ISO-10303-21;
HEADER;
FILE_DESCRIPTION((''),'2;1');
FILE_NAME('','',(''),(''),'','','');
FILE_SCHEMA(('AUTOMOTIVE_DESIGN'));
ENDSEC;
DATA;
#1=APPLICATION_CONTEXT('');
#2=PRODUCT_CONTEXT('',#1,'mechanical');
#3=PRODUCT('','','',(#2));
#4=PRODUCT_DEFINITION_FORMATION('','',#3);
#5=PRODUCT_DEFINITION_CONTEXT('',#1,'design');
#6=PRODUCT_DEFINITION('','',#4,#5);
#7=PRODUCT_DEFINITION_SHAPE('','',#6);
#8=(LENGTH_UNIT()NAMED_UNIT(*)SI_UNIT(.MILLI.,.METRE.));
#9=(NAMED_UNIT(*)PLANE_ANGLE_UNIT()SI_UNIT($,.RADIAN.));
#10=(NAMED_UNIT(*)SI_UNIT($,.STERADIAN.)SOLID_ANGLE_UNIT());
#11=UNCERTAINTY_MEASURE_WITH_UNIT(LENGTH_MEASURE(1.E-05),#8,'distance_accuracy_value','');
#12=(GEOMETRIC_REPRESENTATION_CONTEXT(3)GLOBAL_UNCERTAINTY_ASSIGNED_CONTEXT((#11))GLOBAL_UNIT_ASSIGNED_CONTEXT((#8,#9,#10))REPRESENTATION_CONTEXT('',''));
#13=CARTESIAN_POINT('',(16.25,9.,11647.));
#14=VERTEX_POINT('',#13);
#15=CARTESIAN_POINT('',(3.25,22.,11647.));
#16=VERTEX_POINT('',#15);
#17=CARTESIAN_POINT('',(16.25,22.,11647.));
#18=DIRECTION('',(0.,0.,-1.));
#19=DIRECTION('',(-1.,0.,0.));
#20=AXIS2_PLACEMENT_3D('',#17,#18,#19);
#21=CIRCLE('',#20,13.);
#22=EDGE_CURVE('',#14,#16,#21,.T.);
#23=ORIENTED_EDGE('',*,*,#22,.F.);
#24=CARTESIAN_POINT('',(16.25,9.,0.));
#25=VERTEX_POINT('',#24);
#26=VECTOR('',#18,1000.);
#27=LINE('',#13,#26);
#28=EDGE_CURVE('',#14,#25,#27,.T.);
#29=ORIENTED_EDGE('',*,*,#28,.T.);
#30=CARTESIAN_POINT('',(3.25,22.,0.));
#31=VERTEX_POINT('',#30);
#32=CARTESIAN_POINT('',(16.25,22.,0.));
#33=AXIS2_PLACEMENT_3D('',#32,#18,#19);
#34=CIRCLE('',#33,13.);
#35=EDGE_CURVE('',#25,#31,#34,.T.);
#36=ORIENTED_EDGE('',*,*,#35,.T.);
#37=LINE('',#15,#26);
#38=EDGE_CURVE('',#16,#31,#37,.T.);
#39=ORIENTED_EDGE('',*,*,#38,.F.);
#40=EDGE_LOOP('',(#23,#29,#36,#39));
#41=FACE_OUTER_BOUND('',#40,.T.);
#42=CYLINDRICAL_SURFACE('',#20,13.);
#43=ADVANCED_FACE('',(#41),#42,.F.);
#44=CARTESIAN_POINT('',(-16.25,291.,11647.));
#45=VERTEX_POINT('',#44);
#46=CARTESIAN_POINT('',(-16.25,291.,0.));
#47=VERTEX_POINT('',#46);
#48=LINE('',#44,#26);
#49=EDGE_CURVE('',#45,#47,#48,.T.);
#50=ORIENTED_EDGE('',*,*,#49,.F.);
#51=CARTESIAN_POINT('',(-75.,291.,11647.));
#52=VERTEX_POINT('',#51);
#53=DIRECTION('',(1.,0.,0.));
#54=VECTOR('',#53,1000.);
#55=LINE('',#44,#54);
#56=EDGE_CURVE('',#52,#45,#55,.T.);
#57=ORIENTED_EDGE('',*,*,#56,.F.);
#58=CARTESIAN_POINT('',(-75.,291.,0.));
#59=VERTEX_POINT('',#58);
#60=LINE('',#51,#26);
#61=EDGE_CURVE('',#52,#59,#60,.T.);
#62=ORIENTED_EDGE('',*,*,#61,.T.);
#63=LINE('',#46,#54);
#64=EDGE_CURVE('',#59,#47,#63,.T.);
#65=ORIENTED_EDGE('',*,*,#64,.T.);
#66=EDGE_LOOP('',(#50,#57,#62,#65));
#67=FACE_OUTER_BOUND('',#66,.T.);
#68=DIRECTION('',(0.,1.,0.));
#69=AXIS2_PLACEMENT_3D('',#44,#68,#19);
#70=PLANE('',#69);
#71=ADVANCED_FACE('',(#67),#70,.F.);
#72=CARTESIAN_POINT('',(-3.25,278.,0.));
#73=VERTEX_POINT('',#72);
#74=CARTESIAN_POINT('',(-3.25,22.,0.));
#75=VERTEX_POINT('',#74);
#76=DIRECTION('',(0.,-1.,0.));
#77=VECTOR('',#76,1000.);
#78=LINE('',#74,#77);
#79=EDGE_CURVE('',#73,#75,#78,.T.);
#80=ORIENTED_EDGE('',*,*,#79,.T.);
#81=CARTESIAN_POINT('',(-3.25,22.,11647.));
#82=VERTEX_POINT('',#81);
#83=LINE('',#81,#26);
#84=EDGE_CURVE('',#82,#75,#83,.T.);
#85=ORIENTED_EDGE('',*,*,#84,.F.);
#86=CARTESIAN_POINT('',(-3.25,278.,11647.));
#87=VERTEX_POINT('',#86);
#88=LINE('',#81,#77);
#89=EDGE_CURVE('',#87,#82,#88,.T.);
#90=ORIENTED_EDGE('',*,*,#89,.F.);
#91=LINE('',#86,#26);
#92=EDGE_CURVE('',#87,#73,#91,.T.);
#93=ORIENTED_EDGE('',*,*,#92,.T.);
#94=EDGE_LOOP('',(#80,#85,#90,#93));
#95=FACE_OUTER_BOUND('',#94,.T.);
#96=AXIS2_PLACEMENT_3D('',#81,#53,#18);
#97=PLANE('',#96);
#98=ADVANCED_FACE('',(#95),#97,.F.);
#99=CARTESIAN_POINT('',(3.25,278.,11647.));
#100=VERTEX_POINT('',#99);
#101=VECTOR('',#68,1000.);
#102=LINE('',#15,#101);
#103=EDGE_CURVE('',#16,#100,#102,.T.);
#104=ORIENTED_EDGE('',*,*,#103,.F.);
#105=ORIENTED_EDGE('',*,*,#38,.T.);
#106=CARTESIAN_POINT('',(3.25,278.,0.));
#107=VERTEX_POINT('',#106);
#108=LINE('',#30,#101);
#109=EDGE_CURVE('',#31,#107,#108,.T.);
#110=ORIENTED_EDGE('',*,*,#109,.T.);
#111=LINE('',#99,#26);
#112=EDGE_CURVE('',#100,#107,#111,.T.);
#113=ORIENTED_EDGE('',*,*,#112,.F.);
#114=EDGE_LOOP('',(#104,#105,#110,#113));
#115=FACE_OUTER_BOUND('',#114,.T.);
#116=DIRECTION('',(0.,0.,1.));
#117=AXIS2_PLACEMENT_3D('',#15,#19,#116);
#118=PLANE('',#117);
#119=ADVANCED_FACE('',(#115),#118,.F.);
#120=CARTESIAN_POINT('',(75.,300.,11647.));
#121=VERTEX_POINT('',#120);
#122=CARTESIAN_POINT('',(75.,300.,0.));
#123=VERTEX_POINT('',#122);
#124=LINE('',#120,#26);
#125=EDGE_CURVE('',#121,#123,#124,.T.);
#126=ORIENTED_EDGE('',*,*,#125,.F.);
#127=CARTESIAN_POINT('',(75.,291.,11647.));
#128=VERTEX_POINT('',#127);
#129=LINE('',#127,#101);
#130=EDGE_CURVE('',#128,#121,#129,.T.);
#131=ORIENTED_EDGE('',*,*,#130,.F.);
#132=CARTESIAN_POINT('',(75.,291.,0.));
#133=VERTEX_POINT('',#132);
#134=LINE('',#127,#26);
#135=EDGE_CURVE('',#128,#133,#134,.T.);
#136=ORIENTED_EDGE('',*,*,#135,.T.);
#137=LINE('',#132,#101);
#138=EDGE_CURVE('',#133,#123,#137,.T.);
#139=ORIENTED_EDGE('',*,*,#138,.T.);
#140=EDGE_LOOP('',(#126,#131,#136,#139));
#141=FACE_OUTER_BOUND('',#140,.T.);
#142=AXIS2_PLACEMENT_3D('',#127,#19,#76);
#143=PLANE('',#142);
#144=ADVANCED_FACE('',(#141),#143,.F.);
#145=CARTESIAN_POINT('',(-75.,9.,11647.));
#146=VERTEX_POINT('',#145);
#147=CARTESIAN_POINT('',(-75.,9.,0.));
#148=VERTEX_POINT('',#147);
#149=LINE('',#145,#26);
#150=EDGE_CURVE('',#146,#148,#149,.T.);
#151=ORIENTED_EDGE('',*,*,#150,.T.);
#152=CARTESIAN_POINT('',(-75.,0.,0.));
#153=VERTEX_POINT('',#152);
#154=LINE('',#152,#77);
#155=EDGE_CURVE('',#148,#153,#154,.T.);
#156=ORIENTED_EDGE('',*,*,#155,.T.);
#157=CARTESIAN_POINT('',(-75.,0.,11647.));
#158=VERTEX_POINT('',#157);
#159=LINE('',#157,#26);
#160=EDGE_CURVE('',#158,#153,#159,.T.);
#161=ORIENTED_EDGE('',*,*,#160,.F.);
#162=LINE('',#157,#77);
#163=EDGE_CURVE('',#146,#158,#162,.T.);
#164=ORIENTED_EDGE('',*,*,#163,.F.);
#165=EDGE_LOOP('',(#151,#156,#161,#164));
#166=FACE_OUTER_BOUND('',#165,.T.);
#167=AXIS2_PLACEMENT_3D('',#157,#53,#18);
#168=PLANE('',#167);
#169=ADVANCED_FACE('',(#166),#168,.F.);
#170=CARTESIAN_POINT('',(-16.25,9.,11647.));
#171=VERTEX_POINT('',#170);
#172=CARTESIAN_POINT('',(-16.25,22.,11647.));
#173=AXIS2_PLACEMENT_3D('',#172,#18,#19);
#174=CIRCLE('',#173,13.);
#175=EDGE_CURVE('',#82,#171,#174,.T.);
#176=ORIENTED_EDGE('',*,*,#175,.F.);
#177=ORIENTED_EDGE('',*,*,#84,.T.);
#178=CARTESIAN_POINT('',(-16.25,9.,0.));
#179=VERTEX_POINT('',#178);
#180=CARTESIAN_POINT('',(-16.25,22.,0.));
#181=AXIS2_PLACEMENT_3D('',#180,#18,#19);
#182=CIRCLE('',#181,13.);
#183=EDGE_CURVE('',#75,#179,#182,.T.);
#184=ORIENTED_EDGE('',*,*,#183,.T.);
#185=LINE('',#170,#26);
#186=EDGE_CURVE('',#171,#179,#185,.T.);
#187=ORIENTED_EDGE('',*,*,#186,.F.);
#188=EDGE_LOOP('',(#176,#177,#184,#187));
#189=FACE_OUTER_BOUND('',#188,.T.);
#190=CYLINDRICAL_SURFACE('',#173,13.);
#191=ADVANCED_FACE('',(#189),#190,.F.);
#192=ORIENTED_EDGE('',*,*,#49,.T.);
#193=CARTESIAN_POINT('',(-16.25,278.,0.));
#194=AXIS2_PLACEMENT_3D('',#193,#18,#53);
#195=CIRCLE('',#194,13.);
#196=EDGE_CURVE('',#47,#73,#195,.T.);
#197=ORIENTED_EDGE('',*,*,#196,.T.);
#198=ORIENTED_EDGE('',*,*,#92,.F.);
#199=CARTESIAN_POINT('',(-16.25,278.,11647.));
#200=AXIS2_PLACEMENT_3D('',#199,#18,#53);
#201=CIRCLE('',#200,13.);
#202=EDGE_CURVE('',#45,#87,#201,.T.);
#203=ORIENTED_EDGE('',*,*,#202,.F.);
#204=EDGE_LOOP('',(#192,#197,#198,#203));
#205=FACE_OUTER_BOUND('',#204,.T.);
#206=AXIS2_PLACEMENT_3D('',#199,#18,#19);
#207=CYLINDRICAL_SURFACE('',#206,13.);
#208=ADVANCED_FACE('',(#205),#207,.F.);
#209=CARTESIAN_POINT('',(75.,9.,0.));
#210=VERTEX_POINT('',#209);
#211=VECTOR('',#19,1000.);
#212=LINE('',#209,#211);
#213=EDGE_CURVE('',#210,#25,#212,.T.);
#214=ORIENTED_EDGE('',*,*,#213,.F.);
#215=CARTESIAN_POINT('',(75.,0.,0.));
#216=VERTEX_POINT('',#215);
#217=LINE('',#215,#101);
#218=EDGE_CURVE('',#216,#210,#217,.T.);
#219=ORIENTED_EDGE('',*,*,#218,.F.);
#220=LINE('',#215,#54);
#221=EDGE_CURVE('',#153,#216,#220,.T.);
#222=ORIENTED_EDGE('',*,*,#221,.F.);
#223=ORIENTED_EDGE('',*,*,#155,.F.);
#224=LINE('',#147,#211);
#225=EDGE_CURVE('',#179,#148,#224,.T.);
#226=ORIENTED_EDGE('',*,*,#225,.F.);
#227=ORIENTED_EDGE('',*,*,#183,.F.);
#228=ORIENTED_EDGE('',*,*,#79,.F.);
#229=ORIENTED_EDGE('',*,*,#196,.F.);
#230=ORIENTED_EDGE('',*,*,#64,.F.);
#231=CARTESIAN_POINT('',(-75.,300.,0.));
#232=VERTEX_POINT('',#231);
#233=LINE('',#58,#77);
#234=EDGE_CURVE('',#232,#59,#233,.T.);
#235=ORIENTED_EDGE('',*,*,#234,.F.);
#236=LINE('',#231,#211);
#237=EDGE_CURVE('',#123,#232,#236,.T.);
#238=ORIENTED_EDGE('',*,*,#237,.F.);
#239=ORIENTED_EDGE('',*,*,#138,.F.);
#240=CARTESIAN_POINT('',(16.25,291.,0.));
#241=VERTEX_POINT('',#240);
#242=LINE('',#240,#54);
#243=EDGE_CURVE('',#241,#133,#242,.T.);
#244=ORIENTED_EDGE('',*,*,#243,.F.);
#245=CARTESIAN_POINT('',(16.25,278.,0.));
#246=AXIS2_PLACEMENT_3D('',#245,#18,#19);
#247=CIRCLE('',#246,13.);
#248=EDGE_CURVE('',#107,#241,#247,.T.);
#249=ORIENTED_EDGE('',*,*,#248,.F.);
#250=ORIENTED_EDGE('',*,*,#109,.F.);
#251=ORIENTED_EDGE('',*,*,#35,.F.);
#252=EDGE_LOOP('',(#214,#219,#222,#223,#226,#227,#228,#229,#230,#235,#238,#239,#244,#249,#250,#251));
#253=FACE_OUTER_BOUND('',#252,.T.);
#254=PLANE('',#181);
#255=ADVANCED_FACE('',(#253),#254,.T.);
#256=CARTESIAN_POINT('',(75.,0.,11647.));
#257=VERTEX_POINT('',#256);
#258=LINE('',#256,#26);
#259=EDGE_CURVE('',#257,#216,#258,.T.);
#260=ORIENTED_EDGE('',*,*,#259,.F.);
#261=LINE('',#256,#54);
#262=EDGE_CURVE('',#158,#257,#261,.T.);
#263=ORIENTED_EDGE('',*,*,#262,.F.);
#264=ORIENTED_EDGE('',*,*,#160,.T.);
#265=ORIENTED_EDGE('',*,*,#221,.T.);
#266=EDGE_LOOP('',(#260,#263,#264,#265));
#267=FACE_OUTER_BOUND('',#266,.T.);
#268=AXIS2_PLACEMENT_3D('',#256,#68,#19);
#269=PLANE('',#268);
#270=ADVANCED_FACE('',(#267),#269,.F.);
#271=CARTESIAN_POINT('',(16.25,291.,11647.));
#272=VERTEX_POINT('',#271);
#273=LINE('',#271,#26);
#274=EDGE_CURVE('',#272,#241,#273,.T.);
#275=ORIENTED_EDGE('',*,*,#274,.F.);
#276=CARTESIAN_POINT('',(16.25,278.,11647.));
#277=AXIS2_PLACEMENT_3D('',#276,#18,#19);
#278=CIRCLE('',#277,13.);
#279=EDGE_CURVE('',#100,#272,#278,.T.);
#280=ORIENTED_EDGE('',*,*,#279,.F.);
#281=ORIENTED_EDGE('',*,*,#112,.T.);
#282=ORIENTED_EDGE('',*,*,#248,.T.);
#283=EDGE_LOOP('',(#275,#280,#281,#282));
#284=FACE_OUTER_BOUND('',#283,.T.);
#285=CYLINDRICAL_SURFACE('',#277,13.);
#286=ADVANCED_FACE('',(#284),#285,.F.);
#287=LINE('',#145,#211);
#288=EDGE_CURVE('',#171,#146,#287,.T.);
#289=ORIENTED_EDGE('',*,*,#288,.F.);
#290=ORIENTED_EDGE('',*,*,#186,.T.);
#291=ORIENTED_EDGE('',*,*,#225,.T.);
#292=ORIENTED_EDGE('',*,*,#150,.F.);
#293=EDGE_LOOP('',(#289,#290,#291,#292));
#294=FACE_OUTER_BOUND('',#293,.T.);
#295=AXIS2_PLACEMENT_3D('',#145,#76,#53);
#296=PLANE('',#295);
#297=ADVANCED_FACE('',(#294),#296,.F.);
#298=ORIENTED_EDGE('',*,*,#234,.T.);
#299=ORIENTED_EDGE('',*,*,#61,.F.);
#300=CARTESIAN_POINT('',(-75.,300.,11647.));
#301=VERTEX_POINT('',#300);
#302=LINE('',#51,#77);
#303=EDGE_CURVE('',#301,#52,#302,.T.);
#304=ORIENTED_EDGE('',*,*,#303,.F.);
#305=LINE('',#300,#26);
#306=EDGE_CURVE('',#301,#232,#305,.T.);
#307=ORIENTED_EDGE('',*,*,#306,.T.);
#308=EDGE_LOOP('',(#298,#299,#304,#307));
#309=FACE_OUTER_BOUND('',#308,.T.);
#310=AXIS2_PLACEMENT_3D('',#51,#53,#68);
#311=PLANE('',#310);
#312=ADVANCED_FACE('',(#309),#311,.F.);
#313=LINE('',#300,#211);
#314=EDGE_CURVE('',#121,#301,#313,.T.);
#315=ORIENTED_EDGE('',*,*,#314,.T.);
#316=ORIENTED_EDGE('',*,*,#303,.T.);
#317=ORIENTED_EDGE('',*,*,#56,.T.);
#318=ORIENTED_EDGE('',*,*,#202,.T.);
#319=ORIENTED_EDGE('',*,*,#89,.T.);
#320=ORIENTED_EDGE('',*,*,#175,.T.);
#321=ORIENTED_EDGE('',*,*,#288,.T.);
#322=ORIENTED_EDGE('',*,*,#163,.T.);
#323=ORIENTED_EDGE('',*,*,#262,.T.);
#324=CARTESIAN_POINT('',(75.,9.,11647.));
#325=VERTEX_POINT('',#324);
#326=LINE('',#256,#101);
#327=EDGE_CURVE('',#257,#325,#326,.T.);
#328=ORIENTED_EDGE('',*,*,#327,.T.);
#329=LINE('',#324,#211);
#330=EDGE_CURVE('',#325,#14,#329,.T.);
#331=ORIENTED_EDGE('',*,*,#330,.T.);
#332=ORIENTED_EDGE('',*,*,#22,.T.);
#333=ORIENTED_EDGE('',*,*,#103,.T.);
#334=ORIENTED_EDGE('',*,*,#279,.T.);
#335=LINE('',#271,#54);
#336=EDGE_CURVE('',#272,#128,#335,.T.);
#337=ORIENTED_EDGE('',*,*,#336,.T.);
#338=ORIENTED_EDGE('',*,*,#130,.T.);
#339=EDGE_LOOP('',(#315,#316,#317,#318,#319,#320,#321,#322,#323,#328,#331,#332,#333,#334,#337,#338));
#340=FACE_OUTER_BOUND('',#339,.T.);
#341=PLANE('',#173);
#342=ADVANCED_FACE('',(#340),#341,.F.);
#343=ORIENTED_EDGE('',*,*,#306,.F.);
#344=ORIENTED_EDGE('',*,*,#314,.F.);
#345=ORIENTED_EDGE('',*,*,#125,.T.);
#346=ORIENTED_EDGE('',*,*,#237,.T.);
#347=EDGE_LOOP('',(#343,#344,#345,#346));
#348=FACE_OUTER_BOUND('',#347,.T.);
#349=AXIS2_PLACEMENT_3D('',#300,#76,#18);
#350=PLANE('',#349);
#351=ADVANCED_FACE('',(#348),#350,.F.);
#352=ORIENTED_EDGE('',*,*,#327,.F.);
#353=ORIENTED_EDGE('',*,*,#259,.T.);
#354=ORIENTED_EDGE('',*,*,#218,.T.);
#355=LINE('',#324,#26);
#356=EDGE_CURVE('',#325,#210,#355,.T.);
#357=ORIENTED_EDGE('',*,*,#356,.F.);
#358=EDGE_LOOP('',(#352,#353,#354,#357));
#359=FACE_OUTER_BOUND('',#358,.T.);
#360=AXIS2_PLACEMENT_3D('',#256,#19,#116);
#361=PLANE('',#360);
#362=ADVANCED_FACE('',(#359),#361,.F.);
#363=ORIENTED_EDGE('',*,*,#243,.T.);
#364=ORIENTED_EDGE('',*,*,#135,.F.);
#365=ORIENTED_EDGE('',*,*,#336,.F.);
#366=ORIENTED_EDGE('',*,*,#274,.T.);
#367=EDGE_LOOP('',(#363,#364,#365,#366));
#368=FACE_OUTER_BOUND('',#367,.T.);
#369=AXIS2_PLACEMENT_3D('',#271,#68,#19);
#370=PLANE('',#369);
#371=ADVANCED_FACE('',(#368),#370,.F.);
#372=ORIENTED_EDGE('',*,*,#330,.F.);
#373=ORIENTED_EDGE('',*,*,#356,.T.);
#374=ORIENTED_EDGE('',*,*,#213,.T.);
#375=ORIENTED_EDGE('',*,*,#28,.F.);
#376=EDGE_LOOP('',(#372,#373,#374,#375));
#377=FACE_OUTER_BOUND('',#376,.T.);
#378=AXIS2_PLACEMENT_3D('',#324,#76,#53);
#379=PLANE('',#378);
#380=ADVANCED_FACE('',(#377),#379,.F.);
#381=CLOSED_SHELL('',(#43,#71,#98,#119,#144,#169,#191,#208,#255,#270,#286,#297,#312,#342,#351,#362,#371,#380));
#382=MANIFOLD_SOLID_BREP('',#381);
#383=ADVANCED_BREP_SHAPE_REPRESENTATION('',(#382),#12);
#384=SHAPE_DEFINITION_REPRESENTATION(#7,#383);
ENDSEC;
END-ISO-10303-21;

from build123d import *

# Parameters (mm, degrees)
BOSS_EXTRUDE1_DEPTH = 11647


with BuildPart() as part:
    # Sketch1 → Boss-Extrude1 (new body)
    with BuildSketch(Plane.XY):
        with BuildLine():
            Line((75, 0), (-75, 0))
            Line((-75, 0), (-75, 9))
            Line((-75, 9), (-16.25, 9))
            ThreePointArc((-16.25, 9), (-7.057611845, 12.807611845), (-3.25, 22))
            Line((-3.25, 22), (-3.25, 278))
            ThreePointArc((-3.25, 278), (-7.057611845, 287.192388155), (-16.25, 291))
            Line((-16.25, 291), (-75, 291))
            Line((-75, 291), (-75, 300))
            Line((-75, 300), (75, 300))
            Line((75, 300), (75, 291))
            Line((75, 291), (16.25, 291))
            ThreePointArc((16.25, 291), (7.057611845, 287.192388155), (3.25, 278))
            Line((3.25, 278), (3.25, 22))
            ThreePointArc((3.25, 22), (7.057611845, 12.807611845), (16.25, 9))
            Line((16.25, 9), (75, 9))
            Line((75, 9), (75, 0))
        make_face()
    extrude(amount=BOSS_EXTRUDE1_DEPTH)


solid = part.part
